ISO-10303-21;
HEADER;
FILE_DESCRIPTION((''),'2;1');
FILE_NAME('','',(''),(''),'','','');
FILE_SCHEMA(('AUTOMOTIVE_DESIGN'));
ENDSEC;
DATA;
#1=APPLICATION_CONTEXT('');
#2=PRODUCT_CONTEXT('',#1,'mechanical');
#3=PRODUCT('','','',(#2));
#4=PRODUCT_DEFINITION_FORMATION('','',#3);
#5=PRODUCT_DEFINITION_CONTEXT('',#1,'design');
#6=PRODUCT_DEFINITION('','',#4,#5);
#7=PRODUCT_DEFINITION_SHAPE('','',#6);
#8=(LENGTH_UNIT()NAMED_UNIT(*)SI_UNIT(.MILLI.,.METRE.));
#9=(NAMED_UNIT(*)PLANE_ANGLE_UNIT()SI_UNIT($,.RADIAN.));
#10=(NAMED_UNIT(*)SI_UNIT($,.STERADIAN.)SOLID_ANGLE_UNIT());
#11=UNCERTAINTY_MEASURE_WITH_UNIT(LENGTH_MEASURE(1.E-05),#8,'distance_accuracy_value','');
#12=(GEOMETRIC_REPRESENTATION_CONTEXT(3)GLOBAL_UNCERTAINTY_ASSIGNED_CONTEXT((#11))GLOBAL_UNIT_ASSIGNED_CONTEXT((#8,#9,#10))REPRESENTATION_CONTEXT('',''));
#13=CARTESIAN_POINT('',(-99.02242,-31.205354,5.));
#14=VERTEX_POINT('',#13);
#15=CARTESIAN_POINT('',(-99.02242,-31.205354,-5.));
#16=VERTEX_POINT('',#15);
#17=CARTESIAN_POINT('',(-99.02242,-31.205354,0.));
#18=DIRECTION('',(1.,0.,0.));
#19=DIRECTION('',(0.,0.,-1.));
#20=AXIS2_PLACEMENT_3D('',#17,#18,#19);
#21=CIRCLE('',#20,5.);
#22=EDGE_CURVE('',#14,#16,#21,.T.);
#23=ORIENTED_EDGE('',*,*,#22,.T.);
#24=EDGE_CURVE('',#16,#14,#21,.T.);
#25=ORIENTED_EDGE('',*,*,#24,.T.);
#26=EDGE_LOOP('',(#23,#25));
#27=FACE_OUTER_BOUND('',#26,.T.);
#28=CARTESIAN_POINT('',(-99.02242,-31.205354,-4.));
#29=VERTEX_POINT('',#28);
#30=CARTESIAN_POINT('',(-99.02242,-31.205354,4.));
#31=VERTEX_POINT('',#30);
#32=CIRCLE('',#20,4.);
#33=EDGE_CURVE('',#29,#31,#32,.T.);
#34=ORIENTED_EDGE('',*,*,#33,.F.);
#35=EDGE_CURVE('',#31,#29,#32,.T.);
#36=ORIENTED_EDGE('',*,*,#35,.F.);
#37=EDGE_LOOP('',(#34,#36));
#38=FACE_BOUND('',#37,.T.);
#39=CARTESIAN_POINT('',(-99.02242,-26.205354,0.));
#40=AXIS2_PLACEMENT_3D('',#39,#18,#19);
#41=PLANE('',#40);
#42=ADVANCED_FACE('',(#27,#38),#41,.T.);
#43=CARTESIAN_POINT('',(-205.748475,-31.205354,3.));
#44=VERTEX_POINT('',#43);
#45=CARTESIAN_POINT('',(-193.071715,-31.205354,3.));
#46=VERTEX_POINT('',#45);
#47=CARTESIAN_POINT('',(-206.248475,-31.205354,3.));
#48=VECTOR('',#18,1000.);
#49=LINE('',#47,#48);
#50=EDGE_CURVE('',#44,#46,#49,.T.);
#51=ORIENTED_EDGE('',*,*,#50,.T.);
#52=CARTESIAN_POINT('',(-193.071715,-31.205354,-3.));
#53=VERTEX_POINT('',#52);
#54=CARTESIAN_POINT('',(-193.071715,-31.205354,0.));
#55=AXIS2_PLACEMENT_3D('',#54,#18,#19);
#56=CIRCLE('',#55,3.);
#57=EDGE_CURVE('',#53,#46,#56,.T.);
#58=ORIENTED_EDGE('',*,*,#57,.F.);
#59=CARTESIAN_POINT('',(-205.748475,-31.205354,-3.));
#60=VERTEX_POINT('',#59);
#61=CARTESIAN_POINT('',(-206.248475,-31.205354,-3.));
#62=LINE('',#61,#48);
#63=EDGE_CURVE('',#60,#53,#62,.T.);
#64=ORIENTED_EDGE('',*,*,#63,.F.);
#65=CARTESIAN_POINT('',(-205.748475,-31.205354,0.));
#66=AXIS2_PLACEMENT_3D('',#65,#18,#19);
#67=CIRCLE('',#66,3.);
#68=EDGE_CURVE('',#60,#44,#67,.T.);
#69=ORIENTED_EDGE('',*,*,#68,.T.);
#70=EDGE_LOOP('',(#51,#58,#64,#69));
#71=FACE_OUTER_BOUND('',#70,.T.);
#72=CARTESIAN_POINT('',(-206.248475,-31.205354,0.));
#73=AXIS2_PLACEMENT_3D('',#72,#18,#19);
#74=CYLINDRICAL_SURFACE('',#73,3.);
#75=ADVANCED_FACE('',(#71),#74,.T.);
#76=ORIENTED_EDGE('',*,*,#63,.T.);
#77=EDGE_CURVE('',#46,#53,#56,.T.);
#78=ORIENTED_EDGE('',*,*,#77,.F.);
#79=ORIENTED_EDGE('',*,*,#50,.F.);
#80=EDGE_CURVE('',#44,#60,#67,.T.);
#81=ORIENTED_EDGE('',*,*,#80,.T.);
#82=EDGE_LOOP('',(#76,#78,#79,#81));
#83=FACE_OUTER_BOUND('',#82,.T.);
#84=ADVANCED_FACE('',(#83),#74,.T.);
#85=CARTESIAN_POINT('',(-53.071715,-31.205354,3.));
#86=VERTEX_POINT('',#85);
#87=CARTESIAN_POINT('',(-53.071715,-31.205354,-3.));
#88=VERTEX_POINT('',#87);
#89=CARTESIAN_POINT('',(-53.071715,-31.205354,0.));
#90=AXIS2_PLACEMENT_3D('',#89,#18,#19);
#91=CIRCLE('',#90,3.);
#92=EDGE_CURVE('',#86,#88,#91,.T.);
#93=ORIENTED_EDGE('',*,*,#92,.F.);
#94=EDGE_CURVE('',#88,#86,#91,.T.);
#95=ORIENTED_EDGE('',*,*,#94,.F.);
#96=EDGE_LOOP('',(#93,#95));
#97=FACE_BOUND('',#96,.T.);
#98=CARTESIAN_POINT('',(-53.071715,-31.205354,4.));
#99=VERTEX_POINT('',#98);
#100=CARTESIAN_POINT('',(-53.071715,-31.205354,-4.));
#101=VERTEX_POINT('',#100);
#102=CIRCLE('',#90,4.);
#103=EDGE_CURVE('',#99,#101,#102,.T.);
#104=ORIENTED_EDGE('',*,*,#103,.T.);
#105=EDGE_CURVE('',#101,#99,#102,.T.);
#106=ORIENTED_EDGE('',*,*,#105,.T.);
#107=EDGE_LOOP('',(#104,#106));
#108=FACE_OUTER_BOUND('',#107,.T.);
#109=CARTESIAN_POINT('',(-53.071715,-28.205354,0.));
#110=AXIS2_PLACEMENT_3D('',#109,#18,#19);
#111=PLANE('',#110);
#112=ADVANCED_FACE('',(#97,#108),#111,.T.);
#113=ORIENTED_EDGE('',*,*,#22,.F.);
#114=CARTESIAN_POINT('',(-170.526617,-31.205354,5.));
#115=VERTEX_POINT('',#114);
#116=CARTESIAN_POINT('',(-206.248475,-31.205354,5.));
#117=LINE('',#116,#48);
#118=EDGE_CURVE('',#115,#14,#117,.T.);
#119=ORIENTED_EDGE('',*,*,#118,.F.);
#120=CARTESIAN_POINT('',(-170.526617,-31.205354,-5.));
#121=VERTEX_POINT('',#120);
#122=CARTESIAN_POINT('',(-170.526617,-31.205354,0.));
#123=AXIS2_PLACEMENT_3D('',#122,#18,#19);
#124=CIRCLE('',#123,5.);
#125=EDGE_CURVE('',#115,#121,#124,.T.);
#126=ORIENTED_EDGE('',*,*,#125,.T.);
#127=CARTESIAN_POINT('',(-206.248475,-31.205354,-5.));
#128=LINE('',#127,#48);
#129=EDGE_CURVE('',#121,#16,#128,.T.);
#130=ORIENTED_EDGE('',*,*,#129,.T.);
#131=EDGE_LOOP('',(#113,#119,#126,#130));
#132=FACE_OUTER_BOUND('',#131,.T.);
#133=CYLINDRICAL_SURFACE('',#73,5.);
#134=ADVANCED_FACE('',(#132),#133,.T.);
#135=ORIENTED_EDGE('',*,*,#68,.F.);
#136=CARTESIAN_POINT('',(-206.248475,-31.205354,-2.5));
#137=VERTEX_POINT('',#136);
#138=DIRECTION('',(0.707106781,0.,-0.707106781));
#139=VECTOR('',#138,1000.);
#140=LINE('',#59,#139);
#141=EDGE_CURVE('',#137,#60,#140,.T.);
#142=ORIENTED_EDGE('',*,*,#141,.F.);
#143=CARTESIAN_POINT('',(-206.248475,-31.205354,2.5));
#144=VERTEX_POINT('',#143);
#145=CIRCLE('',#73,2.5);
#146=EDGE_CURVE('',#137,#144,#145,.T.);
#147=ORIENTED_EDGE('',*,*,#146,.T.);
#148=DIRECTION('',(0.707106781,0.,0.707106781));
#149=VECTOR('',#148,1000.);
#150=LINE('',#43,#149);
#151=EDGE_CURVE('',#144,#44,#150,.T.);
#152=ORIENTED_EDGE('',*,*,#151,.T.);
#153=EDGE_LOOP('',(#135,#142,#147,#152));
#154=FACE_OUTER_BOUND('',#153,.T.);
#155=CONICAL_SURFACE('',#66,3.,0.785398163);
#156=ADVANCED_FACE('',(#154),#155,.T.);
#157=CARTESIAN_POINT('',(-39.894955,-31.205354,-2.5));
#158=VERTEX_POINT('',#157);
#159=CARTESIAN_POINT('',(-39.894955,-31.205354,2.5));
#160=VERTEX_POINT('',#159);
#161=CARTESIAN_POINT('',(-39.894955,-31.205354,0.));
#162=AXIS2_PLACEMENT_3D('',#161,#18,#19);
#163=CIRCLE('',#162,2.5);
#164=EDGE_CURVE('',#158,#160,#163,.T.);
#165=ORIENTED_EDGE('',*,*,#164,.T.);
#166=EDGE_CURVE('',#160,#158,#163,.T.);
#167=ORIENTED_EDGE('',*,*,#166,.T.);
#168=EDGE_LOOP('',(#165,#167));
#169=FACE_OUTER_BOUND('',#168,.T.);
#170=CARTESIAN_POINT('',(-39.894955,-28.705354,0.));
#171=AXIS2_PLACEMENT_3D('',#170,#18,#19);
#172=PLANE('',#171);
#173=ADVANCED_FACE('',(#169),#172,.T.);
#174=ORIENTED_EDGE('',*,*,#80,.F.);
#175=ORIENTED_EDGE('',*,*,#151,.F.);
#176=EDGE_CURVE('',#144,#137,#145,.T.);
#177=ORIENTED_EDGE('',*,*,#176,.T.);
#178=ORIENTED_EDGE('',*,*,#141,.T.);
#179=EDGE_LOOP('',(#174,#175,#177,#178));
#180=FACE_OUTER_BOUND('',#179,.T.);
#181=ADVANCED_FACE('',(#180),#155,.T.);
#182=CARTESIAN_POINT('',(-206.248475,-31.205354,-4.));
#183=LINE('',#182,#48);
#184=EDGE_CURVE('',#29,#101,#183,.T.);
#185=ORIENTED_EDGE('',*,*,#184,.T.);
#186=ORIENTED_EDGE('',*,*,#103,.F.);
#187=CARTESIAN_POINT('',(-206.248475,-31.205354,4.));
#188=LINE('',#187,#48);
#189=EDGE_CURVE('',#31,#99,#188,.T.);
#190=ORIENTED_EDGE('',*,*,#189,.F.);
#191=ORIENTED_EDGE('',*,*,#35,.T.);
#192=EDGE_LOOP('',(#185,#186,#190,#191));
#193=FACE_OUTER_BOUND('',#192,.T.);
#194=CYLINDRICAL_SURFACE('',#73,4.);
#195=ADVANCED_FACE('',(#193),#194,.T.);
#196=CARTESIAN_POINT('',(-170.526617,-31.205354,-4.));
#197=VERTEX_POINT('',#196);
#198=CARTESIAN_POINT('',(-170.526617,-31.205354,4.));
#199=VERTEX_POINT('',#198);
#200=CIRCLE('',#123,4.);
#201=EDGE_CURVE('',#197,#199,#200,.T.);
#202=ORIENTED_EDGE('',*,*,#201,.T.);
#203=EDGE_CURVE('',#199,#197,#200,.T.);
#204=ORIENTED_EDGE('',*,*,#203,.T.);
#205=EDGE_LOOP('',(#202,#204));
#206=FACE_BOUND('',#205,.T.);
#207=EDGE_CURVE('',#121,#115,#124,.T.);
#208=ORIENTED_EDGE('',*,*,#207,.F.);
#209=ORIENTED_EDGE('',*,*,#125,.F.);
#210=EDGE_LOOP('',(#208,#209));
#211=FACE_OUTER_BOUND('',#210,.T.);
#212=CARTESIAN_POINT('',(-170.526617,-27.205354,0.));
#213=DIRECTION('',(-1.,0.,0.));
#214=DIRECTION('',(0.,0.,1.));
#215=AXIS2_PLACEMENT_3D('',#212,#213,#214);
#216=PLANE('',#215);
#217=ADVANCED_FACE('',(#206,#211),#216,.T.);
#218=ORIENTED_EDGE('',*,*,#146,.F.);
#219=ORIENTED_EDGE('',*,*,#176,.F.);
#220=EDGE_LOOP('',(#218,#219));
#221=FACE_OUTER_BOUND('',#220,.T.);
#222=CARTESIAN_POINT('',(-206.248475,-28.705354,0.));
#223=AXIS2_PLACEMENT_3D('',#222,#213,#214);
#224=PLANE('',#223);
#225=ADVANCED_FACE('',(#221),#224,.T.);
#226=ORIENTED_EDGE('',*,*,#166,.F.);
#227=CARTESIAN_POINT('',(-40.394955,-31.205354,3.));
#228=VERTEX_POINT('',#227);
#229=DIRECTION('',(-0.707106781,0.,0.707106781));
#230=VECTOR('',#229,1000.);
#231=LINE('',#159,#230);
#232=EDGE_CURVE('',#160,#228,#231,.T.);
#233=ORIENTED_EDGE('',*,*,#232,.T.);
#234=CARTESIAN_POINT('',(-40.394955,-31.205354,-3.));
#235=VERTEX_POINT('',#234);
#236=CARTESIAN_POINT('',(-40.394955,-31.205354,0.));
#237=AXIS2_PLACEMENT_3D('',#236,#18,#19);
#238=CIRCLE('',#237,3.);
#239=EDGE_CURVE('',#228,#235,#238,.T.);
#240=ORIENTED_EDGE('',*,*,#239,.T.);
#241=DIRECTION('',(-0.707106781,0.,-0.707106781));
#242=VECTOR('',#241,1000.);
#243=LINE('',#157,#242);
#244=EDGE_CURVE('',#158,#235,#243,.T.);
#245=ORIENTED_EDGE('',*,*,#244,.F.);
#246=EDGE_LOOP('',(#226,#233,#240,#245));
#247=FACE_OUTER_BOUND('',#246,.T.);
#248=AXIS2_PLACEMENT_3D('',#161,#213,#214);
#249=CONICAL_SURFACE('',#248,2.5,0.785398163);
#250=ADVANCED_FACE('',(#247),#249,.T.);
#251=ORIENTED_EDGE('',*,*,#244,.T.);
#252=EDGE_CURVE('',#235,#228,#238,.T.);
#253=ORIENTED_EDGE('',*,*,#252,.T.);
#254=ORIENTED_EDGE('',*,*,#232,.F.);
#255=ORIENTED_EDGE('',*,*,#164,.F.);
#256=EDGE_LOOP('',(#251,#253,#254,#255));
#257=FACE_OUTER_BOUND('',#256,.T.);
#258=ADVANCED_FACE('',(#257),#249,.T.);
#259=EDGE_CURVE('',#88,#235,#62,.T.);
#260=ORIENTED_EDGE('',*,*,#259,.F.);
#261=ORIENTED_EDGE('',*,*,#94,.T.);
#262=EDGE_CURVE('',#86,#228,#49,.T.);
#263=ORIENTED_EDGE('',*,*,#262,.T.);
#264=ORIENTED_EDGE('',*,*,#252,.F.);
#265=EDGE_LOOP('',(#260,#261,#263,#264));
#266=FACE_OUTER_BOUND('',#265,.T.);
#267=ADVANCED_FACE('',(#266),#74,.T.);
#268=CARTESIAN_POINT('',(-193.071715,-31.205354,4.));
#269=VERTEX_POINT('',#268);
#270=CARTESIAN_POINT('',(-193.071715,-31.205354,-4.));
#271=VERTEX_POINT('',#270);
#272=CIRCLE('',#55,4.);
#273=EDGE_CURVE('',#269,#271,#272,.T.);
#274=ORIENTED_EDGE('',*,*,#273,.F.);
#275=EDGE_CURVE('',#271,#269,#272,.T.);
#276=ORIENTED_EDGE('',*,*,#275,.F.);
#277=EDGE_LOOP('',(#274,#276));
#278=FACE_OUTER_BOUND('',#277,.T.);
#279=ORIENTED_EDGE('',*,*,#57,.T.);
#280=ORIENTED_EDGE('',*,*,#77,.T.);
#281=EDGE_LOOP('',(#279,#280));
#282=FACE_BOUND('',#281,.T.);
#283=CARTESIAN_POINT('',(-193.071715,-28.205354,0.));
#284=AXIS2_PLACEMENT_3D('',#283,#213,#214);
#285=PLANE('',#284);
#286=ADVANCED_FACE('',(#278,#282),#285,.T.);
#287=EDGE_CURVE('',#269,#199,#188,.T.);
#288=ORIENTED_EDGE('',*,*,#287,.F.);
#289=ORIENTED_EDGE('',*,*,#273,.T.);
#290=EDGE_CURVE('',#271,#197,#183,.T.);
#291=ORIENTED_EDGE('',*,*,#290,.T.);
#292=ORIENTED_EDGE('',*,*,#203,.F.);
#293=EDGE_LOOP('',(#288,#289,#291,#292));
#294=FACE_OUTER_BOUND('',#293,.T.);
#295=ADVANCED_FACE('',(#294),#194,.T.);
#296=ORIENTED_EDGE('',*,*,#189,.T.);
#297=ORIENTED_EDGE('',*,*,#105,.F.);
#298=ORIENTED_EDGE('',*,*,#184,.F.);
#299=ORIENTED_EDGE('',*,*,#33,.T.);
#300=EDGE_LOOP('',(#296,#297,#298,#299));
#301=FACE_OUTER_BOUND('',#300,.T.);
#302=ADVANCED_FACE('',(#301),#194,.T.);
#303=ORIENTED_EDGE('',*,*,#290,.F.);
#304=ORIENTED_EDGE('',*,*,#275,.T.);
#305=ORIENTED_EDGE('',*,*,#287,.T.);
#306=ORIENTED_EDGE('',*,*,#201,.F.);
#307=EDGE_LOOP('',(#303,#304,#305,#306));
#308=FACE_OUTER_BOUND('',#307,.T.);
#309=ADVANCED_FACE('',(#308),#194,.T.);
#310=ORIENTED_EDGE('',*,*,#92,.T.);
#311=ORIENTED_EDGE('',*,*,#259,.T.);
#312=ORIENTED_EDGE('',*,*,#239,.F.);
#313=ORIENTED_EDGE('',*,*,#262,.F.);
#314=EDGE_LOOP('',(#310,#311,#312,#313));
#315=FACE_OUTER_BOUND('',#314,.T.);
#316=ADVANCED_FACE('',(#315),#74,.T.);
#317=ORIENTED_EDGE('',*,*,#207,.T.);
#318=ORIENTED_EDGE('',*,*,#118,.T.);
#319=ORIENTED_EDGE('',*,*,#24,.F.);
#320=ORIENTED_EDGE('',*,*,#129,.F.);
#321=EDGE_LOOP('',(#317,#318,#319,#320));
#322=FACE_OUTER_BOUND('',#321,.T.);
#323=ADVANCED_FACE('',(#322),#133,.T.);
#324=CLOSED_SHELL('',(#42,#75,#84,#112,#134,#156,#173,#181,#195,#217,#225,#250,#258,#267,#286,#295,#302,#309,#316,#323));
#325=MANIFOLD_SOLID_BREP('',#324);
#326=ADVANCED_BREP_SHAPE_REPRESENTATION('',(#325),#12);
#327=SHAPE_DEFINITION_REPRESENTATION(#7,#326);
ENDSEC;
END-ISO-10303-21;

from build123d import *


with BuildPart() as part:
    # Model → Revolve1 (revolve)
    with BuildSketch(Plane.XY, mode=Mode.PRIVATE) as revolve1_sk:
        Polygon((-193.071714982, -28.205353865), (-193.071714982, -27.205353865), (-170.52661738, -27.205353865), (-170.52661738, -26.205353865), (-99.022420086, -26.205353865), (-99.022420086, -27.205353865), (-53.071714982, -27.205353865), (-53.071714982, -28.205353865), (-41.671714982, -28.205353865), (-40.394954521, -28.205353865), (-39.894954521, -28.705353865), (-39.894954521, -31.205353865), (-206.248475443, -31.205353865), (-206.248475443, -28.705353865), (-205.748475443, -28.205353865), (-199.071714982, -28.205353865), align=None)
    revolve(revolve1_sk.sketch.rotate(Axis((-206.248475443, -31.205353865, 0), (-1, 0, 0)), 90), axis=Axis((-206.248475443, -31.205353865, 0), (-1, 0, 0)))


solid = part.part
